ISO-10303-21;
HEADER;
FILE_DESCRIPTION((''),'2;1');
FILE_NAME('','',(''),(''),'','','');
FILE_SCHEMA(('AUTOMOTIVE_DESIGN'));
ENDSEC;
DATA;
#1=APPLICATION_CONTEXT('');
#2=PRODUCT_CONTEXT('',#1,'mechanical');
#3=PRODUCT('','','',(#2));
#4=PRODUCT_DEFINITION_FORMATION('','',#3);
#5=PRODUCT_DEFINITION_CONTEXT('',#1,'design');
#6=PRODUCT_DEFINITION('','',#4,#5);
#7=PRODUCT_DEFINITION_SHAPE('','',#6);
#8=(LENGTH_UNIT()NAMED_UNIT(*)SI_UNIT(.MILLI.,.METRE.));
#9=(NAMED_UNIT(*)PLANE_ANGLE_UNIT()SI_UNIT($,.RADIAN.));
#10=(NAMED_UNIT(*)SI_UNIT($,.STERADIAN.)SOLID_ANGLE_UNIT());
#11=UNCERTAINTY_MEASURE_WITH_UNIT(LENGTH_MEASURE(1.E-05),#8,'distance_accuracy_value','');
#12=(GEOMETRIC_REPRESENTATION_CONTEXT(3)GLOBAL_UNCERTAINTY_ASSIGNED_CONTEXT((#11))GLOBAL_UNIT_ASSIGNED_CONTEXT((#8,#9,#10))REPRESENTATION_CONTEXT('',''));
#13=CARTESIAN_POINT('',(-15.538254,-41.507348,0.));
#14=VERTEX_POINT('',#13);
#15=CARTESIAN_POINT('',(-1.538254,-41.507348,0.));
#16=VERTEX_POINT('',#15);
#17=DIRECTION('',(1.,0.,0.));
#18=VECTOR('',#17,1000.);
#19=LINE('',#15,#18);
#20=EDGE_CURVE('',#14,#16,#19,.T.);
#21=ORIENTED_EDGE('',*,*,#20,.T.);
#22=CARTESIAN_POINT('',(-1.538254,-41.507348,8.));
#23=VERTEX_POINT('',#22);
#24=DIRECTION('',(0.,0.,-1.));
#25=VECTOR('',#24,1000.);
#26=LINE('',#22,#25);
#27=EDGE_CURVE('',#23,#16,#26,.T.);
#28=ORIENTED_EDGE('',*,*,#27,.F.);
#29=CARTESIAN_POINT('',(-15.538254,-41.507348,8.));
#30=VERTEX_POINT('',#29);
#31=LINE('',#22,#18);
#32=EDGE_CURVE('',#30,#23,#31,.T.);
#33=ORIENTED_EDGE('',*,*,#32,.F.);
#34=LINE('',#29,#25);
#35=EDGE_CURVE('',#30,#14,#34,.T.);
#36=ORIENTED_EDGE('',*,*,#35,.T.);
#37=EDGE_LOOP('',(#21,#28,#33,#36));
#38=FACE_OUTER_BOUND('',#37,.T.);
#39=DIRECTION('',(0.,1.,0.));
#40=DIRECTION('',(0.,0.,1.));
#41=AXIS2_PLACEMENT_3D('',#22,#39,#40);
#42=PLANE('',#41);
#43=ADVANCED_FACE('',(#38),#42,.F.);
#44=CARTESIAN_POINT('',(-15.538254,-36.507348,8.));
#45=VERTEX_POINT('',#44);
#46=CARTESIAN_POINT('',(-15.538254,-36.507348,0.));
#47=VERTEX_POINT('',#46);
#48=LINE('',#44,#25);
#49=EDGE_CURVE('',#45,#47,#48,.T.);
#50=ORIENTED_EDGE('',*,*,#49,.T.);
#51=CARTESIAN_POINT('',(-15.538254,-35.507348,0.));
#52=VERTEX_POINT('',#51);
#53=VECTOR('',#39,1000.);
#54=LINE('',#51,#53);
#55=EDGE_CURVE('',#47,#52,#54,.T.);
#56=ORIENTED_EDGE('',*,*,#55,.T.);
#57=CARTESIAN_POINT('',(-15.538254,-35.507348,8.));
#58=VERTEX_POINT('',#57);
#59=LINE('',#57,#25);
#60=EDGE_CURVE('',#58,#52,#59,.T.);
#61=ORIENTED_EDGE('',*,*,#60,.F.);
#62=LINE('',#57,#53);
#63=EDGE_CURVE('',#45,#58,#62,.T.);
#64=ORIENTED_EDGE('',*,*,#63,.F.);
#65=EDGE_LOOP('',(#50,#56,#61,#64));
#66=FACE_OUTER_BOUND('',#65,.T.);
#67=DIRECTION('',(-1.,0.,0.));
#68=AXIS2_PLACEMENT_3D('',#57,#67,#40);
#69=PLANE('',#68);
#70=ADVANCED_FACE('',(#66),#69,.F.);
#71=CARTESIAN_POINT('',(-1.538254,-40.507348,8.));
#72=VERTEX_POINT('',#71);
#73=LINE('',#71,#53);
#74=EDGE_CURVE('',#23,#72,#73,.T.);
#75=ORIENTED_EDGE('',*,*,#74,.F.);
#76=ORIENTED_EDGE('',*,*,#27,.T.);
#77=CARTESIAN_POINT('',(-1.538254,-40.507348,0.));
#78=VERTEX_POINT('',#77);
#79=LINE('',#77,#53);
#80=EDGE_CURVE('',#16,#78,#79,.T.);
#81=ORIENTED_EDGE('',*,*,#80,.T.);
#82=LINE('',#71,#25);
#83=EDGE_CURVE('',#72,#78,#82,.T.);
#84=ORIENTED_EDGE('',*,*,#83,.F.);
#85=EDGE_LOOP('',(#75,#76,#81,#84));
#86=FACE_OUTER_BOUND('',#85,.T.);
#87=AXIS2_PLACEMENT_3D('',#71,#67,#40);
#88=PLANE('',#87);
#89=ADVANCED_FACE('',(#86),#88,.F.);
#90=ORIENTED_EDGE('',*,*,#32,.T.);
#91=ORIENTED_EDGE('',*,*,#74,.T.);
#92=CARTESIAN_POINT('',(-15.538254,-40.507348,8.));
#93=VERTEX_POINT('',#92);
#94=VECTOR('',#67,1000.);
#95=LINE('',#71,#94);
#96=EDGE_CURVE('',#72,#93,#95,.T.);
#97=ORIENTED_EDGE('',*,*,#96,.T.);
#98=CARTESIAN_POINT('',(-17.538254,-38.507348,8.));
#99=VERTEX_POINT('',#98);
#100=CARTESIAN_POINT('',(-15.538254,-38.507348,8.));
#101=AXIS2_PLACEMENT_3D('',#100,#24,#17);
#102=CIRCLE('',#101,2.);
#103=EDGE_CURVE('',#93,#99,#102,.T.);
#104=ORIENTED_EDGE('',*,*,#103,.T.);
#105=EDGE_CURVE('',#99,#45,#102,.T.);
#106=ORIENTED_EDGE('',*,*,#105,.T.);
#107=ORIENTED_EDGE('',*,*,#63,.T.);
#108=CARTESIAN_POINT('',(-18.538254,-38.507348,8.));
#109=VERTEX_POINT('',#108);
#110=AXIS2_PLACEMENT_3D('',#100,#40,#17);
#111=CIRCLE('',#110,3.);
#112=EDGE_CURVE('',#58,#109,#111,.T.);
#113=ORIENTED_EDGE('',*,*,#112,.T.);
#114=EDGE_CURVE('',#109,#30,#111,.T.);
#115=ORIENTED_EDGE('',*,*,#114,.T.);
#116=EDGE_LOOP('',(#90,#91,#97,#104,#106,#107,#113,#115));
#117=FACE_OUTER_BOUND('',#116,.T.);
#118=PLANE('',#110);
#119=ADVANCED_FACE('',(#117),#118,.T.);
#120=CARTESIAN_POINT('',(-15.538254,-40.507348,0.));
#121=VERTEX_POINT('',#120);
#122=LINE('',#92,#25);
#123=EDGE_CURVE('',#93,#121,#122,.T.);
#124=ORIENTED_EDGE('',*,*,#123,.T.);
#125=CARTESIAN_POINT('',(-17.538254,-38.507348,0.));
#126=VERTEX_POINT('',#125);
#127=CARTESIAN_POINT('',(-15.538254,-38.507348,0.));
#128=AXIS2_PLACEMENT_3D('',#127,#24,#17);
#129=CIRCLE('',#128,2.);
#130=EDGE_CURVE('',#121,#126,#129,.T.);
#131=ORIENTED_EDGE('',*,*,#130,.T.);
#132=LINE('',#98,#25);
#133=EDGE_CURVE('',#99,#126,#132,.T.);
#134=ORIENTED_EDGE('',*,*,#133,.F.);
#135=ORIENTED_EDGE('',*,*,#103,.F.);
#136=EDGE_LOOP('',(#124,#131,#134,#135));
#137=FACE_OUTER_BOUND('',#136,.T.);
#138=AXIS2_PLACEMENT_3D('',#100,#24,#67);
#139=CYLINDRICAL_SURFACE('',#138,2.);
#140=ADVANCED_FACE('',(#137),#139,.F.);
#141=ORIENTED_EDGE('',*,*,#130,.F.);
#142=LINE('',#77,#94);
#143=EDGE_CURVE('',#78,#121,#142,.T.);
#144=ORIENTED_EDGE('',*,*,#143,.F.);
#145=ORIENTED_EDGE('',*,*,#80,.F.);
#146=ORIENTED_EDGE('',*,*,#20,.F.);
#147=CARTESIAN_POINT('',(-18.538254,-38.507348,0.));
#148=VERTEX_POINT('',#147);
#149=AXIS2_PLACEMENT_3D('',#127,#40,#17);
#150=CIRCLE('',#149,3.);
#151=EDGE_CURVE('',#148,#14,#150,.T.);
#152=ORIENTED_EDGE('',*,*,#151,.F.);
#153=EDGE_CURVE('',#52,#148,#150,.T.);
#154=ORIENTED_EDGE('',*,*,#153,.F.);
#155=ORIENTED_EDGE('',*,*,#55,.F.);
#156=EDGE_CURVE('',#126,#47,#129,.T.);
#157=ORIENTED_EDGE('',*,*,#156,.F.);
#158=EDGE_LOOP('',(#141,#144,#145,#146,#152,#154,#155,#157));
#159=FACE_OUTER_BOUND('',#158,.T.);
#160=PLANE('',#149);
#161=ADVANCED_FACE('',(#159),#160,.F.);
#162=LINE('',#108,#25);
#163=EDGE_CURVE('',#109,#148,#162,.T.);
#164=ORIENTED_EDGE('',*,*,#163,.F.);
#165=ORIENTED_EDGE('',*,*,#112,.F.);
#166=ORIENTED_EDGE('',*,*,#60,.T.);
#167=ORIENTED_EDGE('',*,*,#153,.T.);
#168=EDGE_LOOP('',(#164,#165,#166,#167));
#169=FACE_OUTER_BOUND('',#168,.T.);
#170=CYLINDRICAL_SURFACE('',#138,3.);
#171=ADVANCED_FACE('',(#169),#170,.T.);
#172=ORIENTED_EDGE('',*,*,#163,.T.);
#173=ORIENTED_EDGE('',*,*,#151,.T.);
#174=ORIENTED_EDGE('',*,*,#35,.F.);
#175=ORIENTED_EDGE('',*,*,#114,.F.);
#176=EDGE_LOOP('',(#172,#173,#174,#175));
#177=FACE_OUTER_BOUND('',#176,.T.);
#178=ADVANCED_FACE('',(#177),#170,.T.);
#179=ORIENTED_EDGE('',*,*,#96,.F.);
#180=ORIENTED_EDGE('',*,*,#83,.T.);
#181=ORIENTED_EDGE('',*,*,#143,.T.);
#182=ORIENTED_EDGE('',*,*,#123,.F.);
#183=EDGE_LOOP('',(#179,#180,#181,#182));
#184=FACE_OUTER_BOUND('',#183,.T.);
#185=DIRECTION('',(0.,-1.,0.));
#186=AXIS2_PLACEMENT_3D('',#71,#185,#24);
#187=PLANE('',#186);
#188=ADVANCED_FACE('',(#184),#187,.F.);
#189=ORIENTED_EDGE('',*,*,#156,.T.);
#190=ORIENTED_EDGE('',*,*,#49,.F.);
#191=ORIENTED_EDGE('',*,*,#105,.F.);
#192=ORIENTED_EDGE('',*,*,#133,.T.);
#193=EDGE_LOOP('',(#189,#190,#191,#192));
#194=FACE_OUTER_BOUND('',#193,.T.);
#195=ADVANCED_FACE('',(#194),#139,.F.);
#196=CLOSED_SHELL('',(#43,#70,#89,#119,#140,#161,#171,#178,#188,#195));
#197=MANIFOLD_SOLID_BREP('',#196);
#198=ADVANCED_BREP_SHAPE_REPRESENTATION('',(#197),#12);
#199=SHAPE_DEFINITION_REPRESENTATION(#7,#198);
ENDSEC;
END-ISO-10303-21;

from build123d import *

# Parameters (mm, degrees)
BOSS_EXTRUDE1_DEPTH = 8


with BuildPart() as part:
    # Sketch1 → Boss-Extrude1 (new body)
    with BuildSketch(Plane.XY):
        with BuildLine():
            Line((-1.538253553, -40.507347935), (-15.538253553, -40.507347935))
            ThreePointArc((-15.538253553, -40.507347935), (-17.538253553, -38.507347935), (-15.538253553, -36.507347935))
            Line((-15.538253553, -36.507347935), (-15.538253553, -35.507347935))
            ThreePointArc((-15.538253553, -35.507347935), (-18.538253553, -38.507347935), (-15.538253553, -41.507347935))
            Line((-15.538253553, -41.507347935), (-1.538253553, -41.507347935))
            Line((-1.538253553, -41.507347935), (-1.538253553, -40.507347935))
        make_face()
    extrude(amount=BOSS_EXTRUDE1_DEPTH)


solid = part.part
